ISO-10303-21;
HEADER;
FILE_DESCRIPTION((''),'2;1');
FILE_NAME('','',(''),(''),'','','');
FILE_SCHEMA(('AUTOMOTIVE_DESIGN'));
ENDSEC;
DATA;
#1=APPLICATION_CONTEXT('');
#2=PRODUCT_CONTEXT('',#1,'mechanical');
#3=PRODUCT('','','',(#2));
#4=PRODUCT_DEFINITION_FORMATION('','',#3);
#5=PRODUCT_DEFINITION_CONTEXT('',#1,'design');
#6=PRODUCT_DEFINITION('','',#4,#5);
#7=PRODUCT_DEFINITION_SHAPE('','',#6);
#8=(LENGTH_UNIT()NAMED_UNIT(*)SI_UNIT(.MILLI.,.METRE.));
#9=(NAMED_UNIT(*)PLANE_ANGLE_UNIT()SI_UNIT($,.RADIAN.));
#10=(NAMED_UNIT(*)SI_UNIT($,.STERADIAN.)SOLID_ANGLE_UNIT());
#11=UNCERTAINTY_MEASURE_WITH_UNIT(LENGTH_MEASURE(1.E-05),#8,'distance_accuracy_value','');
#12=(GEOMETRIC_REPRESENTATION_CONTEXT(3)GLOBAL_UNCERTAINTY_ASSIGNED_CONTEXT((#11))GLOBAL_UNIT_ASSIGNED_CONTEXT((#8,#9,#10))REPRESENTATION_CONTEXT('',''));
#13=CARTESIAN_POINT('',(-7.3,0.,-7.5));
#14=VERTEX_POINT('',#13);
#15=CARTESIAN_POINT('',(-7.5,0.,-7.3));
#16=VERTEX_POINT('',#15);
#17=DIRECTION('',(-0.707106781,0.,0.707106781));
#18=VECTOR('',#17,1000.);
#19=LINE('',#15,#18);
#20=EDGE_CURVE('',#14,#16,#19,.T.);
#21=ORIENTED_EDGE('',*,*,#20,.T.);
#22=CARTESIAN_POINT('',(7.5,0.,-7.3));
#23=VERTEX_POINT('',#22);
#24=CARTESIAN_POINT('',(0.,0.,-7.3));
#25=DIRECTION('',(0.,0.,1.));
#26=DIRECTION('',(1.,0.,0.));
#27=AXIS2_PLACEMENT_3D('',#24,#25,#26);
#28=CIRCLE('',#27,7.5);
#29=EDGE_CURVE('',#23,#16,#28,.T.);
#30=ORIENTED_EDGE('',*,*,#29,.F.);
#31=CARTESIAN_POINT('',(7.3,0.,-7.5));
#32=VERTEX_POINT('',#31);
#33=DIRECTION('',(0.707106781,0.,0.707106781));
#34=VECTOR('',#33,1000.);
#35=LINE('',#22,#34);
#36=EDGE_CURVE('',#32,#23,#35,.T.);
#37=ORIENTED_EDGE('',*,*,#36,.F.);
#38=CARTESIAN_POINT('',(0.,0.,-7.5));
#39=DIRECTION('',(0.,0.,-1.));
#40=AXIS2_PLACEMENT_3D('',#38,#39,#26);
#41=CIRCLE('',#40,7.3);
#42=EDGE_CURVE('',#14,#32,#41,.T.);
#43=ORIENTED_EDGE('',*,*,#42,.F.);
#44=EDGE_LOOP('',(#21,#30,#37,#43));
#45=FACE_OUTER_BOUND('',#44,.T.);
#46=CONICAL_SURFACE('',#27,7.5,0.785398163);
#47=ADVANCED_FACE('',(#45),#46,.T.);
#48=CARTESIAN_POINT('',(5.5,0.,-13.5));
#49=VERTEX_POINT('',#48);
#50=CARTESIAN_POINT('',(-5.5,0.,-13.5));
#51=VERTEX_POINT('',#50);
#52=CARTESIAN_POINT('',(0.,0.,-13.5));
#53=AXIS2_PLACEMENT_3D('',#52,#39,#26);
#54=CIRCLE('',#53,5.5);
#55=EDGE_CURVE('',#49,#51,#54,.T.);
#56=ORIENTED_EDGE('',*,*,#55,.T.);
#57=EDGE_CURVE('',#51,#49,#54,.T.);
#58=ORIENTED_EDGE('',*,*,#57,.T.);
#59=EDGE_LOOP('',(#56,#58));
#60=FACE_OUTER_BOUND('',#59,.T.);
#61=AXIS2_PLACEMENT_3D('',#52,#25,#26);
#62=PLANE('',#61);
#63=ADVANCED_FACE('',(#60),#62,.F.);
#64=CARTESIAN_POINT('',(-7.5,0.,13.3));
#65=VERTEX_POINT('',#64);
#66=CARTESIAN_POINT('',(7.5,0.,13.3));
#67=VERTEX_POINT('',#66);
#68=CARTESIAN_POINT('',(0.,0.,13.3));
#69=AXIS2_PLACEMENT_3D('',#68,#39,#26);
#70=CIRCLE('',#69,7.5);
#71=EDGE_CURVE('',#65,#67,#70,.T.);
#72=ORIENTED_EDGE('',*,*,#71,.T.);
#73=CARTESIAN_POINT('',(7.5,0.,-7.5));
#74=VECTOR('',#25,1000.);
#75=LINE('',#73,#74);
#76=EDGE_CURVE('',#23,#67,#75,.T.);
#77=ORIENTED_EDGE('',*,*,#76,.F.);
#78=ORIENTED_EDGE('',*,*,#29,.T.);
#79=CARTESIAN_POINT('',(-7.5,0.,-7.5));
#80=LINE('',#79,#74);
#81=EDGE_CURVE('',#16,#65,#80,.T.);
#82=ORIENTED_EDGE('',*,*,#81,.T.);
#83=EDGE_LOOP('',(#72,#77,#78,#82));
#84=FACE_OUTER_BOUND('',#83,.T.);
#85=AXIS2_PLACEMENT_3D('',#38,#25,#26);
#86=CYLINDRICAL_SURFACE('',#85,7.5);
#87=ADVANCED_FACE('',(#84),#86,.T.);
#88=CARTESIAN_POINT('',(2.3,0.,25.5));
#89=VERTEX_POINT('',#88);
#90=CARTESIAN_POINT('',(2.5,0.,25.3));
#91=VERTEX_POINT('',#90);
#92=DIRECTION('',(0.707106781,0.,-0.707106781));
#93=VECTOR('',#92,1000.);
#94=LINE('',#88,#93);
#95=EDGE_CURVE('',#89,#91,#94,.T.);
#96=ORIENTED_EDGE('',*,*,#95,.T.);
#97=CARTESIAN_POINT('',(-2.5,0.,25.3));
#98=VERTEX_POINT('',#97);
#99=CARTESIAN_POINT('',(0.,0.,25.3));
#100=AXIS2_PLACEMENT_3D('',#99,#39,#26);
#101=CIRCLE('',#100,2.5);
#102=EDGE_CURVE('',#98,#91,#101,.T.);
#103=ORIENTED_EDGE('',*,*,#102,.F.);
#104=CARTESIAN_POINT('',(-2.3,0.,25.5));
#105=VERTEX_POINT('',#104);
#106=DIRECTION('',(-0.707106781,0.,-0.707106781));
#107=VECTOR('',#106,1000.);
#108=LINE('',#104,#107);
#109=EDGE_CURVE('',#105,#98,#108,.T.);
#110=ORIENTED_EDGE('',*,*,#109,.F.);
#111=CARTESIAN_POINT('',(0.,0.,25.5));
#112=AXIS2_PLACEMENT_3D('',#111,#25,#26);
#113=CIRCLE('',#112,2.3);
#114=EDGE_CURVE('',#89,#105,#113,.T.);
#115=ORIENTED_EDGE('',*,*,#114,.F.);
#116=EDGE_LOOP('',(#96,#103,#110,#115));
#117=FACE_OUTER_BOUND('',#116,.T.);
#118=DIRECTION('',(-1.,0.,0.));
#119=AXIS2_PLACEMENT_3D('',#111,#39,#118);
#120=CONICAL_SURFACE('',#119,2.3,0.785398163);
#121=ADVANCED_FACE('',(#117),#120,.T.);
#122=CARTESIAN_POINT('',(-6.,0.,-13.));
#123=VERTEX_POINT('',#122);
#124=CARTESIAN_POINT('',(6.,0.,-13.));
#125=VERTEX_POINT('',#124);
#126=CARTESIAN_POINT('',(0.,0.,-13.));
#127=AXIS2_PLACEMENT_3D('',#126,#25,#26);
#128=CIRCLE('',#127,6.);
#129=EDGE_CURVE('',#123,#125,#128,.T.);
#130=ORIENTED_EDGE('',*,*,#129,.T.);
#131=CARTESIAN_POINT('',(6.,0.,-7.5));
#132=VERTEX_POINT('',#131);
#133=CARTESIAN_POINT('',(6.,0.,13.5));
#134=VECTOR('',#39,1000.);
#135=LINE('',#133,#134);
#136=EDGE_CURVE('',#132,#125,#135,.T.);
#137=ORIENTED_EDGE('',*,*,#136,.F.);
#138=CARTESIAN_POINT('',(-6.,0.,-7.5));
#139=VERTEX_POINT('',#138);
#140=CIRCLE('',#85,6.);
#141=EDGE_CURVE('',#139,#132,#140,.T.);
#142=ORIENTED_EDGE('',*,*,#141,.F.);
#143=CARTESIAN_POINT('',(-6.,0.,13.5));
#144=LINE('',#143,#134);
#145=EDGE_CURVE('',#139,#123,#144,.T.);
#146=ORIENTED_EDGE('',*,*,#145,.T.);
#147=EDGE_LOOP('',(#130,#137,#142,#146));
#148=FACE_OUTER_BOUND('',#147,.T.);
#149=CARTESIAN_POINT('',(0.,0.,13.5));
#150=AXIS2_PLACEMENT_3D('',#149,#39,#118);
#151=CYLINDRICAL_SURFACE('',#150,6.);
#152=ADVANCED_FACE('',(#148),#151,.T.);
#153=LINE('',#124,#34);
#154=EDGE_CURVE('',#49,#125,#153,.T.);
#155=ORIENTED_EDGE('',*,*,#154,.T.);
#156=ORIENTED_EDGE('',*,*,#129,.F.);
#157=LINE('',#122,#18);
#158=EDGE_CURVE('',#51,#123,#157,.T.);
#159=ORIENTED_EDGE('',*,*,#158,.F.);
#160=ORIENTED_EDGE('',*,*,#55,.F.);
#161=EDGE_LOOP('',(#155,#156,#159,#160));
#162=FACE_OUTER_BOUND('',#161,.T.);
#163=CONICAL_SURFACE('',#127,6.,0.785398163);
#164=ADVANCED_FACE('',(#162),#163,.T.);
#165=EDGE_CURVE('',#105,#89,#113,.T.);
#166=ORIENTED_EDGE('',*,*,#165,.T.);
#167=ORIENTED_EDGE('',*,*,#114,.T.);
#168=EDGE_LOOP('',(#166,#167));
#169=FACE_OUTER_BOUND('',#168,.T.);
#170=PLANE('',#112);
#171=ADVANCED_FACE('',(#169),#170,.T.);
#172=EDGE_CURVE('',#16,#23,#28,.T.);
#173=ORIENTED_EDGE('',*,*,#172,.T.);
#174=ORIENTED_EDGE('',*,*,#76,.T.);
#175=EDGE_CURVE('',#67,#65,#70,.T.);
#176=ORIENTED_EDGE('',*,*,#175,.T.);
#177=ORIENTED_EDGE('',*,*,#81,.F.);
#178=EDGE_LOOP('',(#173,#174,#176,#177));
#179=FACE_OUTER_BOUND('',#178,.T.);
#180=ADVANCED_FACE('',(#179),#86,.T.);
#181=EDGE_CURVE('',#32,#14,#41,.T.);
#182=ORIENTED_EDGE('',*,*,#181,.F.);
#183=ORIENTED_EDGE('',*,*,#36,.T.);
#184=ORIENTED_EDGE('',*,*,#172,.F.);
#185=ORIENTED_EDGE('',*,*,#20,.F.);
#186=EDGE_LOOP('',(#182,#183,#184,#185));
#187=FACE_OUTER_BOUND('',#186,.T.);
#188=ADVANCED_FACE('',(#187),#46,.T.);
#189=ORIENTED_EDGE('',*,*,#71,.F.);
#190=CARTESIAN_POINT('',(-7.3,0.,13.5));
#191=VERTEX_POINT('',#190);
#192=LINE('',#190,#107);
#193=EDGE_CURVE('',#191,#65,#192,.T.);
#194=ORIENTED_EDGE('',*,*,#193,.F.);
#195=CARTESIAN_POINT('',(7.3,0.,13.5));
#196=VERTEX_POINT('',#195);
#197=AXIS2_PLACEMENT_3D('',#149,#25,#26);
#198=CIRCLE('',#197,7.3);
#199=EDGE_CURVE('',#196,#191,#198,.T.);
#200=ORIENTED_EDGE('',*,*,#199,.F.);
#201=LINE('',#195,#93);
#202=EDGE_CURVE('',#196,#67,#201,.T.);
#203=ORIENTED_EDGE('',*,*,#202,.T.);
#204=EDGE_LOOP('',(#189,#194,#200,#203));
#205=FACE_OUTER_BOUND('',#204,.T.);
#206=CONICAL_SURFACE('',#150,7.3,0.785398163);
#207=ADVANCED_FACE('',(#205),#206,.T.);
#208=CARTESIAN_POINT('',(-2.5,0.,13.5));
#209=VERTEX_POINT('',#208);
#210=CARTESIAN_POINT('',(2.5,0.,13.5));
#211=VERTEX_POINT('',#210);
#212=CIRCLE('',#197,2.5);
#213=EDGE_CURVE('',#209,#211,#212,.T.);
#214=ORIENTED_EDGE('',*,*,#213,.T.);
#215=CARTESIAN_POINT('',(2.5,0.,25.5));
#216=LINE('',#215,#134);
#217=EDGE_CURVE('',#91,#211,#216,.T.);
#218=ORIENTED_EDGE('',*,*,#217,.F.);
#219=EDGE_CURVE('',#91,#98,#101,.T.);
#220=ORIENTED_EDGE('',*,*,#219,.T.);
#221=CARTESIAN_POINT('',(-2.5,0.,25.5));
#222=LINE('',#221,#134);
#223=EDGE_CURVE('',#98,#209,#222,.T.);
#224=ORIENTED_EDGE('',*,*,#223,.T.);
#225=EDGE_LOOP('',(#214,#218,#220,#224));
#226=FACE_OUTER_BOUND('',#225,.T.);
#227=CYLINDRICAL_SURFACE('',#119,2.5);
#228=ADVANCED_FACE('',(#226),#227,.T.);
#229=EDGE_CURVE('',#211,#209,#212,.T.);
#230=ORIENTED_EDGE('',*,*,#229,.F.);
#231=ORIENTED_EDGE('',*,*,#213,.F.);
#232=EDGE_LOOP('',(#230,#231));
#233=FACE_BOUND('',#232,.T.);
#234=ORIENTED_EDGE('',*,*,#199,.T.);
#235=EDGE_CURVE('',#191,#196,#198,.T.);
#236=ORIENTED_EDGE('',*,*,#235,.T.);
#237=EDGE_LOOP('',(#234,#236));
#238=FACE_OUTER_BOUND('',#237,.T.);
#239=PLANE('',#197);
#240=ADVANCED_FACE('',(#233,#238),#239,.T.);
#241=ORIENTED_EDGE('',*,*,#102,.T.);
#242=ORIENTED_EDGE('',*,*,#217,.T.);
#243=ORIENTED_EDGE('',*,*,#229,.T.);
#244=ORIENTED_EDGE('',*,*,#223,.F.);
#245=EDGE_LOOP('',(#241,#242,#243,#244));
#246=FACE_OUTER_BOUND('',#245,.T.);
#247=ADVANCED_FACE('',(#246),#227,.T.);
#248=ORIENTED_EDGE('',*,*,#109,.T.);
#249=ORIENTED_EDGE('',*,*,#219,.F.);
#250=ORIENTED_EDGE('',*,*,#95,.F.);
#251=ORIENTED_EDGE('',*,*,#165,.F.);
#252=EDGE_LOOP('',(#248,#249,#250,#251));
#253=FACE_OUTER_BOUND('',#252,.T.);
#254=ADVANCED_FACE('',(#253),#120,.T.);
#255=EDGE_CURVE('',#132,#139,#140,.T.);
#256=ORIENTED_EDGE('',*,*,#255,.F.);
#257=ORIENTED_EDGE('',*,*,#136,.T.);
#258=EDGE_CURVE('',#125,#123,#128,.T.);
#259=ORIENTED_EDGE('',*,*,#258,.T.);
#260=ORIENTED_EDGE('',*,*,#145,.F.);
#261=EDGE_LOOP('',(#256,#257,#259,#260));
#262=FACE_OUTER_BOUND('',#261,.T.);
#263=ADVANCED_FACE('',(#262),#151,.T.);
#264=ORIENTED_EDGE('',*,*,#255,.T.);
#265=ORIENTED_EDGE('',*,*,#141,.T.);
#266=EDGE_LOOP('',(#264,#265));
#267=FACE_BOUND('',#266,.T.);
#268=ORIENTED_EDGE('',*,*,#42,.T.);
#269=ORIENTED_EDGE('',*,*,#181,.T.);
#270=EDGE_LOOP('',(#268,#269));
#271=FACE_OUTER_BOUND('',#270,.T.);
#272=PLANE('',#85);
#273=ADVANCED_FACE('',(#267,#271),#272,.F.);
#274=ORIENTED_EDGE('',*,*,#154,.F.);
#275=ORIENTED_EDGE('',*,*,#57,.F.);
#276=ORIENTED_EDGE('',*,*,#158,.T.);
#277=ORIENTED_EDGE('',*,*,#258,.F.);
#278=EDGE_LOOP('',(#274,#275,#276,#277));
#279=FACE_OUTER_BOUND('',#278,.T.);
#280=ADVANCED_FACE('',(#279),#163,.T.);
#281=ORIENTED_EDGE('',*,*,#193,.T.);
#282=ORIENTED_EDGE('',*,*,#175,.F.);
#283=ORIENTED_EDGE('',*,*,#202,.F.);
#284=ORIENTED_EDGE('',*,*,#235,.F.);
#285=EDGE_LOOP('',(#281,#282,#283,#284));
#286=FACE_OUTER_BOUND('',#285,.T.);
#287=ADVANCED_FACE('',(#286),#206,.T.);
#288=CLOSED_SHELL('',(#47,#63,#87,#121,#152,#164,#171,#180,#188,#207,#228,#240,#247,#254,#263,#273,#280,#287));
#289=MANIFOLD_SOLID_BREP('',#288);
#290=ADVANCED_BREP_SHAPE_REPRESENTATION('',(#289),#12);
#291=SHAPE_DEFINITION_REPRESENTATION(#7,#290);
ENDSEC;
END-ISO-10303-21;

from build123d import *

# Parameters (mm, degrees)
SKETCH_1_R      = 6
EXTRUDE_1_DEPTH = 13.5
CHAMFER_1_SIZE  = 0.5
SKETCH_2_R      = 2.5
EXTRUDE_2_DEPTH = 12
CHAMFER_2_SIZE  = 0.2
SKETCH_3_R      = 7.5
EXTRUDE_3_DEPTH = 21
CHAMFER_3_SIZE  = 0.2


with BuildPart() as part:
    # 草图1 → 凸台-拉伸1 (new, symmetric)
    with BuildSketch(Plane.XY):
        Circle(SKETCH_1_R)
    extrude(amount=EXTRUDE_1_DEPTH, both=True)

    # 倒角1
    chamfer_1_edges = [part.edges().sort_by_distance(p)[0] for p in [
        (-6, 0, -13.5),
        (-6, 0, 13.5),
    ]]
    chamfer(chamfer_1_edges, length=CHAMFER_1_SIZE)

    # 草图2 → 凸台-拉伸2 (add)
    with BuildSketch(Plane.XY.offset(13.5)):
        Circle(SKETCH_2_R)
    extrude(amount=EXTRUDE_2_DEPTH)

    # 倒角2
    chamfer_2_edges = [part.edges().sort_by_distance(p)[0] for p in [
        (-2.5, 0, 25.5),
    ]]
    chamfer(chamfer_2_edges, length=CHAMFER_2_SIZE)

    # 草图3 → 凸台-拉伸3 (add)
    with BuildSketch(Plane.XY.offset(13.5)):
        Circle(SKETCH_3_R)
    extrude(amount=-EXTRUDE_3_DEPTH)

    # 倒角3
    chamfer_3_edges = [part.edges().sort_by_distance(p)[0] for p in [
        (-7.5, 0, 13.5),
        (-7.5, 0, -7.5),
    ]]
    chamfer(chamfer_3_edges, length=CHAMFER_3_SIZE)


solid = part.part
